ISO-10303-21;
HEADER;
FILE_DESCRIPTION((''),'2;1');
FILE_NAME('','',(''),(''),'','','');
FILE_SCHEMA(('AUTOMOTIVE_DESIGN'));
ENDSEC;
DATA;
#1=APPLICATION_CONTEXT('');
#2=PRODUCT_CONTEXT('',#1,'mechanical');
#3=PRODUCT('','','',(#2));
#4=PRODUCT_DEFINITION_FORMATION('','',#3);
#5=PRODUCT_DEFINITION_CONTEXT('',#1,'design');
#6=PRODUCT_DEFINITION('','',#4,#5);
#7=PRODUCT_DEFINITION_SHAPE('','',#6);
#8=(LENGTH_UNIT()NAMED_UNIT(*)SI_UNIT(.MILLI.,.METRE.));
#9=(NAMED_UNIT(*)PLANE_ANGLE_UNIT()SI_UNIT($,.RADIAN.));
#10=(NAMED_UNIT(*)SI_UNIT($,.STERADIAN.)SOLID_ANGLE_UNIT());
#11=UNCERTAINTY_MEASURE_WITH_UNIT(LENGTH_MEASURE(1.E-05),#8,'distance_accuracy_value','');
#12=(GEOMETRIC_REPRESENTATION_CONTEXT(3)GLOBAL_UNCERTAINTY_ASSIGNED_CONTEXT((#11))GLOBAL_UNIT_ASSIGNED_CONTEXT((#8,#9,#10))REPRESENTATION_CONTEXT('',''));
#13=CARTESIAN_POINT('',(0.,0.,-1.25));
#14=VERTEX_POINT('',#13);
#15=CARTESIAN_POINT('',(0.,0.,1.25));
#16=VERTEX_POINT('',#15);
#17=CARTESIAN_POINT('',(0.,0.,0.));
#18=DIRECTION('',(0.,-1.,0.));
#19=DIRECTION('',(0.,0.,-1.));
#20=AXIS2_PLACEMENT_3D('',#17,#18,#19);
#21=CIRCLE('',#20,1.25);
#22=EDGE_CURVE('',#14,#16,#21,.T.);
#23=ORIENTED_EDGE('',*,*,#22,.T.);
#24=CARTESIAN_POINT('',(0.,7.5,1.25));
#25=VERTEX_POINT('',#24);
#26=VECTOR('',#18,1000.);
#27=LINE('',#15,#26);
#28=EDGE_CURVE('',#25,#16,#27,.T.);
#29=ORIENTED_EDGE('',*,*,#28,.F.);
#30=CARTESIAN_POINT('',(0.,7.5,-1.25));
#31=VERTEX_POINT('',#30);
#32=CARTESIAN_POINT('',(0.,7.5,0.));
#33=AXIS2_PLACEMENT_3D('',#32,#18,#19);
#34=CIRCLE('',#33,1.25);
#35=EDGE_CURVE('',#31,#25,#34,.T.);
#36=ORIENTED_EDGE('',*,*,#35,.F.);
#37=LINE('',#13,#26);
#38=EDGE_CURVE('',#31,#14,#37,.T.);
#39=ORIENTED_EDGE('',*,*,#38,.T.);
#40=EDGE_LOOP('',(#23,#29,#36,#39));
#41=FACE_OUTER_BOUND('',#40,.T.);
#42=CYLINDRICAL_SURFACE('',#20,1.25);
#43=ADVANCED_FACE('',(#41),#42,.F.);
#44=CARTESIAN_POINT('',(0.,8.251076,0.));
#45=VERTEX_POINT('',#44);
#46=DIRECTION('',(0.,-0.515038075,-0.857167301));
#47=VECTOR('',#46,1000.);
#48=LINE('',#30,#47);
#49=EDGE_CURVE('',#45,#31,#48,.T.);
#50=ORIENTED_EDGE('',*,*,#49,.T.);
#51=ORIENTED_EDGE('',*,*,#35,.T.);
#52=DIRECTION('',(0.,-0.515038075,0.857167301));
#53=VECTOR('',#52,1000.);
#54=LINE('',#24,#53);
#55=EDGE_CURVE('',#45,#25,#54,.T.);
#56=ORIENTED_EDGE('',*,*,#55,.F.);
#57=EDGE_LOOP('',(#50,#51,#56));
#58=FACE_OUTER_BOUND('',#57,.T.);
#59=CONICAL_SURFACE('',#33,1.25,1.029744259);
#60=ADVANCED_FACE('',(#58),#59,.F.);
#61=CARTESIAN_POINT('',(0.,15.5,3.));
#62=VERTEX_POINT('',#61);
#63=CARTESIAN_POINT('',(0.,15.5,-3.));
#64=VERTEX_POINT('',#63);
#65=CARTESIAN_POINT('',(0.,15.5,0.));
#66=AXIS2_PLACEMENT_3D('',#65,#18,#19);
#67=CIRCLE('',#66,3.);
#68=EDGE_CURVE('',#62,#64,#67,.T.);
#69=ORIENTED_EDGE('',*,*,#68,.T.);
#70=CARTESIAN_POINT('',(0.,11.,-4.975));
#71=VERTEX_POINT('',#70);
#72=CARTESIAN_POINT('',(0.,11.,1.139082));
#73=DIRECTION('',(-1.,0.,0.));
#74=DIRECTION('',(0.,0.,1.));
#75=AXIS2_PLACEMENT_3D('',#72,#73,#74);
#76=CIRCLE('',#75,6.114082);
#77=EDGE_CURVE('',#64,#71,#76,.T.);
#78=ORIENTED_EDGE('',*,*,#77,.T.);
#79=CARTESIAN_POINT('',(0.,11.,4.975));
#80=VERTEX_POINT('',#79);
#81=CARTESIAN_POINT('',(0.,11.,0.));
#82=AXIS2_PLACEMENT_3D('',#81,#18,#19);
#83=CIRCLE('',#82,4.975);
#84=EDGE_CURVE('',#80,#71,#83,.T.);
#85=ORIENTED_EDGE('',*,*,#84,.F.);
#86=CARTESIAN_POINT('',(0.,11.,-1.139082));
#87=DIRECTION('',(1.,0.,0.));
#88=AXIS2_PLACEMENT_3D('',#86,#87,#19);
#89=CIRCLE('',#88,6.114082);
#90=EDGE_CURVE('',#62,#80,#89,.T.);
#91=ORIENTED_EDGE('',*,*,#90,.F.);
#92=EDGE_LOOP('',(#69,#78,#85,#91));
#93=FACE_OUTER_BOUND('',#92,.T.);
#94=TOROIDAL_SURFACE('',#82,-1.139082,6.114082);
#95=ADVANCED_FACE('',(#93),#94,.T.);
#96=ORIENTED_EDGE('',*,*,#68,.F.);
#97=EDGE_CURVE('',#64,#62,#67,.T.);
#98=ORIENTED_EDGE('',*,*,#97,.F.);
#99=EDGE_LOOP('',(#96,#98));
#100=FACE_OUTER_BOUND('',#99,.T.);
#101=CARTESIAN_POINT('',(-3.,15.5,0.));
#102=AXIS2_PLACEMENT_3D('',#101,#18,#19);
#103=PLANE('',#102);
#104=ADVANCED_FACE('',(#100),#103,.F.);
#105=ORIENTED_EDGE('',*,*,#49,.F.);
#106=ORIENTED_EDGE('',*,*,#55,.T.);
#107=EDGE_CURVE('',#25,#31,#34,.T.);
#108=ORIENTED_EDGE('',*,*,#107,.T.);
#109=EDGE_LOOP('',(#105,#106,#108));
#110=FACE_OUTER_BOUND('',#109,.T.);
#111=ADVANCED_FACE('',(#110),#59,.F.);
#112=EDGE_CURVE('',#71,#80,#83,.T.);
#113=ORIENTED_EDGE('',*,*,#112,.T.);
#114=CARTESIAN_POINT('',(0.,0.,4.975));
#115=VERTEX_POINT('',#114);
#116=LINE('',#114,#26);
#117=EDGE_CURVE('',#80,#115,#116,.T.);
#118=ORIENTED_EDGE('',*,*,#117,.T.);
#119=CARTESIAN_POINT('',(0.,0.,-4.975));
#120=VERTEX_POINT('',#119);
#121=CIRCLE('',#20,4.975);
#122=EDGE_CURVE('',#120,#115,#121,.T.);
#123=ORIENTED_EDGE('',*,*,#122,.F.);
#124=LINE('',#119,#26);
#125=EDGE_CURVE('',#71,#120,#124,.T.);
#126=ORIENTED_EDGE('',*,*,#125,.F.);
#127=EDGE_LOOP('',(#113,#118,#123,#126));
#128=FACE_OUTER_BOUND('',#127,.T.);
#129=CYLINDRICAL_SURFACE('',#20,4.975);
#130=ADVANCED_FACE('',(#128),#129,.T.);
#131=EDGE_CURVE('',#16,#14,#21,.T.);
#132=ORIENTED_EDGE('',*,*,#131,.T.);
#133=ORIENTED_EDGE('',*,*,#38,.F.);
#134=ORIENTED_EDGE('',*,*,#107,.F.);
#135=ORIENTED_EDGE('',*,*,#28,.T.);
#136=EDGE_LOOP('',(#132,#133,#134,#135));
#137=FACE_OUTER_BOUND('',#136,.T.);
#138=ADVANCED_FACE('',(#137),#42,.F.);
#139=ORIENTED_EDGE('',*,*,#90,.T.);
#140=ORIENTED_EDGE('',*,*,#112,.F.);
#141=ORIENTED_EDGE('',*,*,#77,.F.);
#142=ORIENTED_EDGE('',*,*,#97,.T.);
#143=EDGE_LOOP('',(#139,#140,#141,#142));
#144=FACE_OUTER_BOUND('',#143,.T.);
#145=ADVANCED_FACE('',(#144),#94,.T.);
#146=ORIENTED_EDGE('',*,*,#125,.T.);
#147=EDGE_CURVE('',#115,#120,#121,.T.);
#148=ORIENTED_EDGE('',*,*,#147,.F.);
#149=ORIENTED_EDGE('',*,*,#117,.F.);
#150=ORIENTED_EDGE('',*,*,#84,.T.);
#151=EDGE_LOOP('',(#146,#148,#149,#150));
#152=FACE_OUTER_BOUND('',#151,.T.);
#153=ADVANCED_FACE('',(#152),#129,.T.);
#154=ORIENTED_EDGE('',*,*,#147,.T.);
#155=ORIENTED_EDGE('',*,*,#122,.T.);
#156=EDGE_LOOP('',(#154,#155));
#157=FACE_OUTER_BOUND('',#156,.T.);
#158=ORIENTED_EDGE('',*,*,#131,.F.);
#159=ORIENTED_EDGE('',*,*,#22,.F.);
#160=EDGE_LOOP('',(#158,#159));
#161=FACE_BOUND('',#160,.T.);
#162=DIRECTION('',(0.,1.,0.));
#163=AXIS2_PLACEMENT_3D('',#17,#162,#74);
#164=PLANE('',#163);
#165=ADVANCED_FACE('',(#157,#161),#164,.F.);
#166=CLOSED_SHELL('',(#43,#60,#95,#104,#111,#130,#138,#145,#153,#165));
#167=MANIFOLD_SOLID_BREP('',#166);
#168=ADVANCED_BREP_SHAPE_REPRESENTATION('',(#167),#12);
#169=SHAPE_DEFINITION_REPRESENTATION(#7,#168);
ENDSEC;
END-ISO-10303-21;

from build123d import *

# Parameters (mm, degrees)
M3_TAPPED_HOLE1_D     = 2.5
M3_TAPPED_HOLE1_DEPTH = 7.5
M3_TAPPED_HOLE1_TIP   = 0.751075774


with BuildPart() as part:
    # Sketch1 → Revolve1 (revolve)
    with BuildSketch(Plane.XY, mode=Mode.PRIVATE) as revolve1_sk:
        with BuildLine():
            Line((0, 0), (-4.975, 0))
            Line((-4.975, 0), (-4.975, 11))
            ThreePointArc((-4.975, 11), (-4.459519856, 13.45716427), (-3, 15.5))
            Line((-3, 15.5), (0, 15.5))
            Line((0, 15.5), (0, 0))
        make_face()
    revolve(revolve1_sk.sketch.rotate(Axis((0, 0, 0), (0, 1, 0)), 270), axis=Axis((0, 0, 0), (0, 1, 0)))

    # M3 Tapped Hole1
    with Locations(Plane(origin=(0, 0, 0), x_dir=(-1, 0, 0), z_dir=(0, -1, 0))):
        with Locations((0, 0)):
            Hole(M3_TAPPED_HOLE1_D / 2, depth=M3_TAPPED_HOLE1_DEPTH)
            with Locations((0, 0, -(M3_TAPPED_HOLE1_DEPTH + M3_TAPPED_HOLE1_TIP / 2))):  # 118° drill point
                Cone(0, M3_TAPPED_HOLE1_D / 2, M3_TAPPED_HOLE1_TIP, mode=Mode.SUBTRACT)


solid = part.part
